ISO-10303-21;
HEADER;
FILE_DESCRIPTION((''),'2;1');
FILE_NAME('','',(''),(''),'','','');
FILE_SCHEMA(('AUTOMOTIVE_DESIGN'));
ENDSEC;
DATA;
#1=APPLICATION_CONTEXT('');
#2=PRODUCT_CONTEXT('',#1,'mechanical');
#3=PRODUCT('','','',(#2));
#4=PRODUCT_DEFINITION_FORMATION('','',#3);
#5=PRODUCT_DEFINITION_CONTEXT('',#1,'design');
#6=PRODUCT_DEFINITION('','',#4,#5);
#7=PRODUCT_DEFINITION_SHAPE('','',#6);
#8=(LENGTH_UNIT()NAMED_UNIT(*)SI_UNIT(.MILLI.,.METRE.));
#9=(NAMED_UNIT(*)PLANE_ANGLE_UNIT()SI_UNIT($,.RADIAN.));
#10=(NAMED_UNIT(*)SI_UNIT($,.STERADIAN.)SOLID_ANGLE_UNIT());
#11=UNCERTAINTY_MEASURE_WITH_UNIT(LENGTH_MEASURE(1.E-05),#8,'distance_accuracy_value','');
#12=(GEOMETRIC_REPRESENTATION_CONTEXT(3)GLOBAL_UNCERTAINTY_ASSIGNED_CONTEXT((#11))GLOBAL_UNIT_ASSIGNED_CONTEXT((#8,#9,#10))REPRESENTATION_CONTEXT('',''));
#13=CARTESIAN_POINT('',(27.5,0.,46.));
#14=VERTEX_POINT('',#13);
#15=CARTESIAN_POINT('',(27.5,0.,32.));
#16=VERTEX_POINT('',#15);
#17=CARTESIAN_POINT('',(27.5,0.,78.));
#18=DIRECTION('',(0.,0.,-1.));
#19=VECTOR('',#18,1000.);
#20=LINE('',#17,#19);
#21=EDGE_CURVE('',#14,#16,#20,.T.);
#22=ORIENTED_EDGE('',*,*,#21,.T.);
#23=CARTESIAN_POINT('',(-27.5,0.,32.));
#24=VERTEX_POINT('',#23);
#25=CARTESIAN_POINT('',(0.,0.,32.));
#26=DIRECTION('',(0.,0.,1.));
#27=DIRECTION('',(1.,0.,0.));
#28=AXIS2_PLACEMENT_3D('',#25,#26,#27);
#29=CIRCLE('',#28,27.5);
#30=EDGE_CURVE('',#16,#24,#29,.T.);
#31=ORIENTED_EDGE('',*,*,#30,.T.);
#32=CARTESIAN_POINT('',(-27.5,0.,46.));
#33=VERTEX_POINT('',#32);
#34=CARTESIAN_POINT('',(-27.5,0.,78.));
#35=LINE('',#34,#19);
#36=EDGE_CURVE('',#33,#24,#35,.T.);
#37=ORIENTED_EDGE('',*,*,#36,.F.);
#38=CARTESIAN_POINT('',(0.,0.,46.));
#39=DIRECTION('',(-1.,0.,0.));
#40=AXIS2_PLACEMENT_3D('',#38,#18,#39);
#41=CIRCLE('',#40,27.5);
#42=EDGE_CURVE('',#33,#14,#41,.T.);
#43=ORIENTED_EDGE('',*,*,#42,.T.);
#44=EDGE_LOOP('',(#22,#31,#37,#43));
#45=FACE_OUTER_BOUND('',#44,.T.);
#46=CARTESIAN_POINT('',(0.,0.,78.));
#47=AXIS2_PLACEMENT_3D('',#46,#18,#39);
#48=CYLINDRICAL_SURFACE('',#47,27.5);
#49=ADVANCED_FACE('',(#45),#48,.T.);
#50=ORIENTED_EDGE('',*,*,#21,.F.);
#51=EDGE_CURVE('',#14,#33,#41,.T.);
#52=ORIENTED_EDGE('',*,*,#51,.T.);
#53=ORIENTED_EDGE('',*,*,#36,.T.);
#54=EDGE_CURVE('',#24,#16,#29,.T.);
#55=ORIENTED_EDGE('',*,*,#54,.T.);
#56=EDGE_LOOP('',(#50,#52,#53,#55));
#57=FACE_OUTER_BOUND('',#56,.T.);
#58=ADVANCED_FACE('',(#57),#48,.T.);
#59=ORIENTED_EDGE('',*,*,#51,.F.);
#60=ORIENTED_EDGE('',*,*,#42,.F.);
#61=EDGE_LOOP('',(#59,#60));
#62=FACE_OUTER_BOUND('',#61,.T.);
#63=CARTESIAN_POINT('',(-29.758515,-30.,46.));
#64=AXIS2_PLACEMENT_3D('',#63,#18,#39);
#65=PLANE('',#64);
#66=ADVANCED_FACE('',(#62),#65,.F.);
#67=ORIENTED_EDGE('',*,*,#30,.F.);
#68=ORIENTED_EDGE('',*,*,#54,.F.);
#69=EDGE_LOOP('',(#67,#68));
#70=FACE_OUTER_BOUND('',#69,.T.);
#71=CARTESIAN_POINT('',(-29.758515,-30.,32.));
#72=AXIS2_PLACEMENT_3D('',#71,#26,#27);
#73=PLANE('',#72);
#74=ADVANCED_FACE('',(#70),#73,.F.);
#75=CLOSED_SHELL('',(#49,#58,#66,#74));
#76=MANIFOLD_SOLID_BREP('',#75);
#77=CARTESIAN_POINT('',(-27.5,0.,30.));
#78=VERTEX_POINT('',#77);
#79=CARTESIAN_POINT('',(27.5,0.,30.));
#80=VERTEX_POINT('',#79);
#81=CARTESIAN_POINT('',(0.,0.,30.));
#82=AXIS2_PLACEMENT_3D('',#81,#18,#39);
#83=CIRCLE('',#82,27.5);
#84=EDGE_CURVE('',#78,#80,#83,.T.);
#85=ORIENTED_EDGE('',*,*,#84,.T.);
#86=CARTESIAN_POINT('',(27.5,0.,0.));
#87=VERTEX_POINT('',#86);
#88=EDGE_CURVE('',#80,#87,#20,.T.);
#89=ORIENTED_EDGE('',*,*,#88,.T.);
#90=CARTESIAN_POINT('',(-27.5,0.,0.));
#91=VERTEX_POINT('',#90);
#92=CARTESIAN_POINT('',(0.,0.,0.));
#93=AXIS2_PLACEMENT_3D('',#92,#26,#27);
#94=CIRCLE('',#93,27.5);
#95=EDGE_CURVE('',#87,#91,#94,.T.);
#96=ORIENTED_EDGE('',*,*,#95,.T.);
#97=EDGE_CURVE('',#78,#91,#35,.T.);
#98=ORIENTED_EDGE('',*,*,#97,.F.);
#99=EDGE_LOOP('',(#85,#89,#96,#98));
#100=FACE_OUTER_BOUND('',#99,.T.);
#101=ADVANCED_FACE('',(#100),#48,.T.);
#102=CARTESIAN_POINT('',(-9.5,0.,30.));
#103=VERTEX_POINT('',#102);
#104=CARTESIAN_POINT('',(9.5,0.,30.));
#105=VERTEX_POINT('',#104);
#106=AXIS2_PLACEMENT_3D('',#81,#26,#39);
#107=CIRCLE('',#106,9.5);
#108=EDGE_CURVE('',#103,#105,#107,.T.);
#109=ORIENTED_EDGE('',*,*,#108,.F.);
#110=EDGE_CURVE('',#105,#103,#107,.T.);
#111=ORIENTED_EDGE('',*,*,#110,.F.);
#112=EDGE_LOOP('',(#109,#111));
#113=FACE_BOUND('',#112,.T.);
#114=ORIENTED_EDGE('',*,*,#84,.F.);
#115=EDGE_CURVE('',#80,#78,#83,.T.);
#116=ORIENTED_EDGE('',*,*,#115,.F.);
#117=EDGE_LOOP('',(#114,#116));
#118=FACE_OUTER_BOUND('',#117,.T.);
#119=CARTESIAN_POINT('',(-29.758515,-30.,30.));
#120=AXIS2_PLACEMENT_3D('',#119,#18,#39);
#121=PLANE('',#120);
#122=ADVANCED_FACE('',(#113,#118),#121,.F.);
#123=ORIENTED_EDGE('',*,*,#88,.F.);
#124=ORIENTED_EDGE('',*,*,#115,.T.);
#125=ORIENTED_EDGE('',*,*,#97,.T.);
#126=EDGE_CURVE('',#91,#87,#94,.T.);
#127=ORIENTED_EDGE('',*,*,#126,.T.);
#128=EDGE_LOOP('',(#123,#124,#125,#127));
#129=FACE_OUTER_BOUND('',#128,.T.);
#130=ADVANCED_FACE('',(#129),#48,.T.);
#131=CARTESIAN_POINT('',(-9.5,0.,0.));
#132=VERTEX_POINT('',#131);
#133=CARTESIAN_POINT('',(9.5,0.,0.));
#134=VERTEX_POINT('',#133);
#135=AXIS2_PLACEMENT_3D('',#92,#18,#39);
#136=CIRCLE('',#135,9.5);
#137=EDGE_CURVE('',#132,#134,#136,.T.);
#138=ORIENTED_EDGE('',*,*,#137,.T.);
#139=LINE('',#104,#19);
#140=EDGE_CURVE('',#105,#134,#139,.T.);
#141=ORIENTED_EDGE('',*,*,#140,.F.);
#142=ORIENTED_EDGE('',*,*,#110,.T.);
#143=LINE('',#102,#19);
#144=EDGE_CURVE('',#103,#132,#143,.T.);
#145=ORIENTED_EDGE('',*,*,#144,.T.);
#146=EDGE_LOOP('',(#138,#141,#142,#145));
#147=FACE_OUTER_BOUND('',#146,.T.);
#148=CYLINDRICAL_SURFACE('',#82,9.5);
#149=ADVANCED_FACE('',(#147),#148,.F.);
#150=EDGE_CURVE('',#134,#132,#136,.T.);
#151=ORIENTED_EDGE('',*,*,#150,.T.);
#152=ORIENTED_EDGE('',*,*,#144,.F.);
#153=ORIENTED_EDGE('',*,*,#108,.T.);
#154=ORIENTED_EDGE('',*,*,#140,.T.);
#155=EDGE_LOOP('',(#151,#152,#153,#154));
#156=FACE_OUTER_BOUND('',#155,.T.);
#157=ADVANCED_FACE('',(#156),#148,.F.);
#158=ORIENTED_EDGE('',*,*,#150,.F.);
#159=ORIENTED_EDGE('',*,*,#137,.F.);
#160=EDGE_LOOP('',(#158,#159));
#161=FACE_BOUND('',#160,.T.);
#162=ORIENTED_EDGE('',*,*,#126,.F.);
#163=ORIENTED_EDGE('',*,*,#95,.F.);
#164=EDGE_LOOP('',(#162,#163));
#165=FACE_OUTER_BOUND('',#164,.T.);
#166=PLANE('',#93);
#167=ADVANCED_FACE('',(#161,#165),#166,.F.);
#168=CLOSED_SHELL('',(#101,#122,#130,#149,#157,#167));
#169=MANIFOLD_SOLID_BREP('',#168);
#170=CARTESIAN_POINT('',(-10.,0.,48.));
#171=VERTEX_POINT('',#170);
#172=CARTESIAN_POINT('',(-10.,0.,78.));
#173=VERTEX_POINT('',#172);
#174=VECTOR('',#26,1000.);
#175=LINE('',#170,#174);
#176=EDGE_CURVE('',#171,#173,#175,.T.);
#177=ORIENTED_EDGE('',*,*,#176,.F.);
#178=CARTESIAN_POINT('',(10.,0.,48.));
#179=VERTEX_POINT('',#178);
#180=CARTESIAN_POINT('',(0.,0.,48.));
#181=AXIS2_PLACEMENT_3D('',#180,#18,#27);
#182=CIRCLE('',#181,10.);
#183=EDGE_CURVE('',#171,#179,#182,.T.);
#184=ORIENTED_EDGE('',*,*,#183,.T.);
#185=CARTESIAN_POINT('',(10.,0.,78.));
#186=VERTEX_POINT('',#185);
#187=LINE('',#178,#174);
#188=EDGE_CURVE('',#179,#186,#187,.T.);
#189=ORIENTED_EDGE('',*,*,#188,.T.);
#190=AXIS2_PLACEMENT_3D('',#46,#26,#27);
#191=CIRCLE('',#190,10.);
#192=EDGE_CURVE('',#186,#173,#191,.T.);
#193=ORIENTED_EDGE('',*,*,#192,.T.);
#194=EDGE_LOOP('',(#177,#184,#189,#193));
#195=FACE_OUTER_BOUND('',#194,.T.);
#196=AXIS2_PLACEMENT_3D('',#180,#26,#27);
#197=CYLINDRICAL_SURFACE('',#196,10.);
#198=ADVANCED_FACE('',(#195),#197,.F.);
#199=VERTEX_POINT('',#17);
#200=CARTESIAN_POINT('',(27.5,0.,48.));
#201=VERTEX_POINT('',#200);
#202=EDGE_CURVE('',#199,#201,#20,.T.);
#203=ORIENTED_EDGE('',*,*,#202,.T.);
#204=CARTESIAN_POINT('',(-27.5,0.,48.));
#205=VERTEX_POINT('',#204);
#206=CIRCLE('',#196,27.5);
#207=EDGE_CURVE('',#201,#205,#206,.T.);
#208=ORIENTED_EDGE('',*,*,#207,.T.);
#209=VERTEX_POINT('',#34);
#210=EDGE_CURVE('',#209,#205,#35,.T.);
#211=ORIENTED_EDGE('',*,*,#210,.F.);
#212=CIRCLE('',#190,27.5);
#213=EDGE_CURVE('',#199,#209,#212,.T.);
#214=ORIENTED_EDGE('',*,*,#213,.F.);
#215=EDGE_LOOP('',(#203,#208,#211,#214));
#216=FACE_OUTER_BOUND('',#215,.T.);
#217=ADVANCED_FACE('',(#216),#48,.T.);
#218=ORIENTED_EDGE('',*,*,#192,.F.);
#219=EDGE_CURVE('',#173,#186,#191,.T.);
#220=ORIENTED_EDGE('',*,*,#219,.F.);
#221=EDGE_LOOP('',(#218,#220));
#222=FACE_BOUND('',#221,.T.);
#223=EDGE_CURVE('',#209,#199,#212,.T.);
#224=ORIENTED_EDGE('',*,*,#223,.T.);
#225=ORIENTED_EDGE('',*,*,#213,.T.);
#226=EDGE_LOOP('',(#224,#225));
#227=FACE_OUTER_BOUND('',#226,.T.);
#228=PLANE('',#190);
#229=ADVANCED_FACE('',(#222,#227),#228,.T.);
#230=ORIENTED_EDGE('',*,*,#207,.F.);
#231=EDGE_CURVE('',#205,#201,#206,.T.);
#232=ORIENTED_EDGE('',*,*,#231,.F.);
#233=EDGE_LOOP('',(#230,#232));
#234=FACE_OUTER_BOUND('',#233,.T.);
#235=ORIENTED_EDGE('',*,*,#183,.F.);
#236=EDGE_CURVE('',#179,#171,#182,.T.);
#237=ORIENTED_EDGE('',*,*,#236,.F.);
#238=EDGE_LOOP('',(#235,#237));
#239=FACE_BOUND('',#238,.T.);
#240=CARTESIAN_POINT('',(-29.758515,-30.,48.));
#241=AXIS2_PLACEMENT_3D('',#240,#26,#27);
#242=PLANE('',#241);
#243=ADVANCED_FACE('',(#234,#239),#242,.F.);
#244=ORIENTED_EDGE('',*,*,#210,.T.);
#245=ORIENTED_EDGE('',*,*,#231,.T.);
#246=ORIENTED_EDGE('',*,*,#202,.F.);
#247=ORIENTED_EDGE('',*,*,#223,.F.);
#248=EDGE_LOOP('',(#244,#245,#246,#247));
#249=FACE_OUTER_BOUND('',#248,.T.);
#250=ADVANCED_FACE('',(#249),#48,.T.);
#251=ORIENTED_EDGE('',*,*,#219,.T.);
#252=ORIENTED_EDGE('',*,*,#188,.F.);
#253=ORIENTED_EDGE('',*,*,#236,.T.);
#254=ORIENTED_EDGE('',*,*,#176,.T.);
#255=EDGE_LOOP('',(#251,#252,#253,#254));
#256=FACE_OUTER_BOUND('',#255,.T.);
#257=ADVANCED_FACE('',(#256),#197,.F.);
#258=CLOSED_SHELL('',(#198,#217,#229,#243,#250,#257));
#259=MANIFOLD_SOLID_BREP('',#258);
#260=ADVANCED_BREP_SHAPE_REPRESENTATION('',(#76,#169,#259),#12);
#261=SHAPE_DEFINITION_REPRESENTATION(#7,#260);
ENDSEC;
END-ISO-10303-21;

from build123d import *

# Parameters (mm, degrees)
SKETCH1_R           = 27.5
BOSS_EXTRUDE1_DEPTH = 78
SKETCH2_R           = 10
CUT_EXTRUDE1_DEPTH  = 30
SKETCH3_R           = 9.5
CUT_EXTRUDE2_DEPTH  = 30
SKETCH4_W           = 61.293657596
SKETCH4_H           = 2
CUT_EXTRUDE3_DEPTH  = 30


with BuildPart() as part:
    # Sketch1 → Boss-Extrude1 (new body)
    with BuildSketch(Plane.XY):
        Circle(SKETCH1_R)
    extrude(amount=BOSS_EXTRUDE1_DEPTH)

    # Sketch2 → Cut-Extrude1 (cut)
    with BuildSketch(Plane.XY.offset(78)):
        Circle(SKETCH2_R)
    extrude(amount=-CUT_EXTRUDE1_DEPTH, mode=Mode.SUBTRACT)

    # Sketch3 → Cut-Extrude2 (cut)
    with BuildSketch(Plane(origin=(0, 0, 0), x_dir=(-1, 0, 0), z_dir=(0, 0, -1))):
        Circle(SKETCH3_R)
    extrude(amount=-CUT_EXTRUDE2_DEPTH, mode=Mode.SUBTRACT)

    # Sketch4 → Cut-Extrude3 (cut, symmetric)
    with BuildSketch(Plane(origin=(0, 0, 0), x_dir=(1, 0, 0), z_dir=(0, 1, 0))):
        with Locations((0.888313878, -31)):
            Rectangle(SKETCH4_W, SKETCH4_H)
        with Locations((0.888313878, -47)):
            Rectangle(SKETCH4_W, SKETCH4_H)
    extrude(amount=CUT_EXTRUDE3_DEPTH, both=True, mode=Mode.SUBTRACT)


with BuildPart() as cut_extrude3_piece_1:
    # of the separate pieces the step leaves, piece 1, a body of its own (cut_extrude3_pieces)
    add(part.part.solids().sort_by_distance((27.5, 0, 0))[0])


with BuildPart() as cut_extrude3_piece_2:
    # of the separate pieces the step leaves, piece 2, a body of its own (cut_extrude3_pieces)
    add(part.part.solids().sort_by_distance((27.5, 0, 48))[0])


with BuildPart() as cut_extrude3_piece_3:
    # of the separate pieces the step leaves, piece 3, a body of its own (cut_extrude3_pieces)
    add(part.part.solids().sort_by_distance((27.5, 0, 32))[0])


solid = Compound([cut_extrude3_piece_1.part, cut_extrude3_piece_2.part, cut_extrude3_piece_3.part])
